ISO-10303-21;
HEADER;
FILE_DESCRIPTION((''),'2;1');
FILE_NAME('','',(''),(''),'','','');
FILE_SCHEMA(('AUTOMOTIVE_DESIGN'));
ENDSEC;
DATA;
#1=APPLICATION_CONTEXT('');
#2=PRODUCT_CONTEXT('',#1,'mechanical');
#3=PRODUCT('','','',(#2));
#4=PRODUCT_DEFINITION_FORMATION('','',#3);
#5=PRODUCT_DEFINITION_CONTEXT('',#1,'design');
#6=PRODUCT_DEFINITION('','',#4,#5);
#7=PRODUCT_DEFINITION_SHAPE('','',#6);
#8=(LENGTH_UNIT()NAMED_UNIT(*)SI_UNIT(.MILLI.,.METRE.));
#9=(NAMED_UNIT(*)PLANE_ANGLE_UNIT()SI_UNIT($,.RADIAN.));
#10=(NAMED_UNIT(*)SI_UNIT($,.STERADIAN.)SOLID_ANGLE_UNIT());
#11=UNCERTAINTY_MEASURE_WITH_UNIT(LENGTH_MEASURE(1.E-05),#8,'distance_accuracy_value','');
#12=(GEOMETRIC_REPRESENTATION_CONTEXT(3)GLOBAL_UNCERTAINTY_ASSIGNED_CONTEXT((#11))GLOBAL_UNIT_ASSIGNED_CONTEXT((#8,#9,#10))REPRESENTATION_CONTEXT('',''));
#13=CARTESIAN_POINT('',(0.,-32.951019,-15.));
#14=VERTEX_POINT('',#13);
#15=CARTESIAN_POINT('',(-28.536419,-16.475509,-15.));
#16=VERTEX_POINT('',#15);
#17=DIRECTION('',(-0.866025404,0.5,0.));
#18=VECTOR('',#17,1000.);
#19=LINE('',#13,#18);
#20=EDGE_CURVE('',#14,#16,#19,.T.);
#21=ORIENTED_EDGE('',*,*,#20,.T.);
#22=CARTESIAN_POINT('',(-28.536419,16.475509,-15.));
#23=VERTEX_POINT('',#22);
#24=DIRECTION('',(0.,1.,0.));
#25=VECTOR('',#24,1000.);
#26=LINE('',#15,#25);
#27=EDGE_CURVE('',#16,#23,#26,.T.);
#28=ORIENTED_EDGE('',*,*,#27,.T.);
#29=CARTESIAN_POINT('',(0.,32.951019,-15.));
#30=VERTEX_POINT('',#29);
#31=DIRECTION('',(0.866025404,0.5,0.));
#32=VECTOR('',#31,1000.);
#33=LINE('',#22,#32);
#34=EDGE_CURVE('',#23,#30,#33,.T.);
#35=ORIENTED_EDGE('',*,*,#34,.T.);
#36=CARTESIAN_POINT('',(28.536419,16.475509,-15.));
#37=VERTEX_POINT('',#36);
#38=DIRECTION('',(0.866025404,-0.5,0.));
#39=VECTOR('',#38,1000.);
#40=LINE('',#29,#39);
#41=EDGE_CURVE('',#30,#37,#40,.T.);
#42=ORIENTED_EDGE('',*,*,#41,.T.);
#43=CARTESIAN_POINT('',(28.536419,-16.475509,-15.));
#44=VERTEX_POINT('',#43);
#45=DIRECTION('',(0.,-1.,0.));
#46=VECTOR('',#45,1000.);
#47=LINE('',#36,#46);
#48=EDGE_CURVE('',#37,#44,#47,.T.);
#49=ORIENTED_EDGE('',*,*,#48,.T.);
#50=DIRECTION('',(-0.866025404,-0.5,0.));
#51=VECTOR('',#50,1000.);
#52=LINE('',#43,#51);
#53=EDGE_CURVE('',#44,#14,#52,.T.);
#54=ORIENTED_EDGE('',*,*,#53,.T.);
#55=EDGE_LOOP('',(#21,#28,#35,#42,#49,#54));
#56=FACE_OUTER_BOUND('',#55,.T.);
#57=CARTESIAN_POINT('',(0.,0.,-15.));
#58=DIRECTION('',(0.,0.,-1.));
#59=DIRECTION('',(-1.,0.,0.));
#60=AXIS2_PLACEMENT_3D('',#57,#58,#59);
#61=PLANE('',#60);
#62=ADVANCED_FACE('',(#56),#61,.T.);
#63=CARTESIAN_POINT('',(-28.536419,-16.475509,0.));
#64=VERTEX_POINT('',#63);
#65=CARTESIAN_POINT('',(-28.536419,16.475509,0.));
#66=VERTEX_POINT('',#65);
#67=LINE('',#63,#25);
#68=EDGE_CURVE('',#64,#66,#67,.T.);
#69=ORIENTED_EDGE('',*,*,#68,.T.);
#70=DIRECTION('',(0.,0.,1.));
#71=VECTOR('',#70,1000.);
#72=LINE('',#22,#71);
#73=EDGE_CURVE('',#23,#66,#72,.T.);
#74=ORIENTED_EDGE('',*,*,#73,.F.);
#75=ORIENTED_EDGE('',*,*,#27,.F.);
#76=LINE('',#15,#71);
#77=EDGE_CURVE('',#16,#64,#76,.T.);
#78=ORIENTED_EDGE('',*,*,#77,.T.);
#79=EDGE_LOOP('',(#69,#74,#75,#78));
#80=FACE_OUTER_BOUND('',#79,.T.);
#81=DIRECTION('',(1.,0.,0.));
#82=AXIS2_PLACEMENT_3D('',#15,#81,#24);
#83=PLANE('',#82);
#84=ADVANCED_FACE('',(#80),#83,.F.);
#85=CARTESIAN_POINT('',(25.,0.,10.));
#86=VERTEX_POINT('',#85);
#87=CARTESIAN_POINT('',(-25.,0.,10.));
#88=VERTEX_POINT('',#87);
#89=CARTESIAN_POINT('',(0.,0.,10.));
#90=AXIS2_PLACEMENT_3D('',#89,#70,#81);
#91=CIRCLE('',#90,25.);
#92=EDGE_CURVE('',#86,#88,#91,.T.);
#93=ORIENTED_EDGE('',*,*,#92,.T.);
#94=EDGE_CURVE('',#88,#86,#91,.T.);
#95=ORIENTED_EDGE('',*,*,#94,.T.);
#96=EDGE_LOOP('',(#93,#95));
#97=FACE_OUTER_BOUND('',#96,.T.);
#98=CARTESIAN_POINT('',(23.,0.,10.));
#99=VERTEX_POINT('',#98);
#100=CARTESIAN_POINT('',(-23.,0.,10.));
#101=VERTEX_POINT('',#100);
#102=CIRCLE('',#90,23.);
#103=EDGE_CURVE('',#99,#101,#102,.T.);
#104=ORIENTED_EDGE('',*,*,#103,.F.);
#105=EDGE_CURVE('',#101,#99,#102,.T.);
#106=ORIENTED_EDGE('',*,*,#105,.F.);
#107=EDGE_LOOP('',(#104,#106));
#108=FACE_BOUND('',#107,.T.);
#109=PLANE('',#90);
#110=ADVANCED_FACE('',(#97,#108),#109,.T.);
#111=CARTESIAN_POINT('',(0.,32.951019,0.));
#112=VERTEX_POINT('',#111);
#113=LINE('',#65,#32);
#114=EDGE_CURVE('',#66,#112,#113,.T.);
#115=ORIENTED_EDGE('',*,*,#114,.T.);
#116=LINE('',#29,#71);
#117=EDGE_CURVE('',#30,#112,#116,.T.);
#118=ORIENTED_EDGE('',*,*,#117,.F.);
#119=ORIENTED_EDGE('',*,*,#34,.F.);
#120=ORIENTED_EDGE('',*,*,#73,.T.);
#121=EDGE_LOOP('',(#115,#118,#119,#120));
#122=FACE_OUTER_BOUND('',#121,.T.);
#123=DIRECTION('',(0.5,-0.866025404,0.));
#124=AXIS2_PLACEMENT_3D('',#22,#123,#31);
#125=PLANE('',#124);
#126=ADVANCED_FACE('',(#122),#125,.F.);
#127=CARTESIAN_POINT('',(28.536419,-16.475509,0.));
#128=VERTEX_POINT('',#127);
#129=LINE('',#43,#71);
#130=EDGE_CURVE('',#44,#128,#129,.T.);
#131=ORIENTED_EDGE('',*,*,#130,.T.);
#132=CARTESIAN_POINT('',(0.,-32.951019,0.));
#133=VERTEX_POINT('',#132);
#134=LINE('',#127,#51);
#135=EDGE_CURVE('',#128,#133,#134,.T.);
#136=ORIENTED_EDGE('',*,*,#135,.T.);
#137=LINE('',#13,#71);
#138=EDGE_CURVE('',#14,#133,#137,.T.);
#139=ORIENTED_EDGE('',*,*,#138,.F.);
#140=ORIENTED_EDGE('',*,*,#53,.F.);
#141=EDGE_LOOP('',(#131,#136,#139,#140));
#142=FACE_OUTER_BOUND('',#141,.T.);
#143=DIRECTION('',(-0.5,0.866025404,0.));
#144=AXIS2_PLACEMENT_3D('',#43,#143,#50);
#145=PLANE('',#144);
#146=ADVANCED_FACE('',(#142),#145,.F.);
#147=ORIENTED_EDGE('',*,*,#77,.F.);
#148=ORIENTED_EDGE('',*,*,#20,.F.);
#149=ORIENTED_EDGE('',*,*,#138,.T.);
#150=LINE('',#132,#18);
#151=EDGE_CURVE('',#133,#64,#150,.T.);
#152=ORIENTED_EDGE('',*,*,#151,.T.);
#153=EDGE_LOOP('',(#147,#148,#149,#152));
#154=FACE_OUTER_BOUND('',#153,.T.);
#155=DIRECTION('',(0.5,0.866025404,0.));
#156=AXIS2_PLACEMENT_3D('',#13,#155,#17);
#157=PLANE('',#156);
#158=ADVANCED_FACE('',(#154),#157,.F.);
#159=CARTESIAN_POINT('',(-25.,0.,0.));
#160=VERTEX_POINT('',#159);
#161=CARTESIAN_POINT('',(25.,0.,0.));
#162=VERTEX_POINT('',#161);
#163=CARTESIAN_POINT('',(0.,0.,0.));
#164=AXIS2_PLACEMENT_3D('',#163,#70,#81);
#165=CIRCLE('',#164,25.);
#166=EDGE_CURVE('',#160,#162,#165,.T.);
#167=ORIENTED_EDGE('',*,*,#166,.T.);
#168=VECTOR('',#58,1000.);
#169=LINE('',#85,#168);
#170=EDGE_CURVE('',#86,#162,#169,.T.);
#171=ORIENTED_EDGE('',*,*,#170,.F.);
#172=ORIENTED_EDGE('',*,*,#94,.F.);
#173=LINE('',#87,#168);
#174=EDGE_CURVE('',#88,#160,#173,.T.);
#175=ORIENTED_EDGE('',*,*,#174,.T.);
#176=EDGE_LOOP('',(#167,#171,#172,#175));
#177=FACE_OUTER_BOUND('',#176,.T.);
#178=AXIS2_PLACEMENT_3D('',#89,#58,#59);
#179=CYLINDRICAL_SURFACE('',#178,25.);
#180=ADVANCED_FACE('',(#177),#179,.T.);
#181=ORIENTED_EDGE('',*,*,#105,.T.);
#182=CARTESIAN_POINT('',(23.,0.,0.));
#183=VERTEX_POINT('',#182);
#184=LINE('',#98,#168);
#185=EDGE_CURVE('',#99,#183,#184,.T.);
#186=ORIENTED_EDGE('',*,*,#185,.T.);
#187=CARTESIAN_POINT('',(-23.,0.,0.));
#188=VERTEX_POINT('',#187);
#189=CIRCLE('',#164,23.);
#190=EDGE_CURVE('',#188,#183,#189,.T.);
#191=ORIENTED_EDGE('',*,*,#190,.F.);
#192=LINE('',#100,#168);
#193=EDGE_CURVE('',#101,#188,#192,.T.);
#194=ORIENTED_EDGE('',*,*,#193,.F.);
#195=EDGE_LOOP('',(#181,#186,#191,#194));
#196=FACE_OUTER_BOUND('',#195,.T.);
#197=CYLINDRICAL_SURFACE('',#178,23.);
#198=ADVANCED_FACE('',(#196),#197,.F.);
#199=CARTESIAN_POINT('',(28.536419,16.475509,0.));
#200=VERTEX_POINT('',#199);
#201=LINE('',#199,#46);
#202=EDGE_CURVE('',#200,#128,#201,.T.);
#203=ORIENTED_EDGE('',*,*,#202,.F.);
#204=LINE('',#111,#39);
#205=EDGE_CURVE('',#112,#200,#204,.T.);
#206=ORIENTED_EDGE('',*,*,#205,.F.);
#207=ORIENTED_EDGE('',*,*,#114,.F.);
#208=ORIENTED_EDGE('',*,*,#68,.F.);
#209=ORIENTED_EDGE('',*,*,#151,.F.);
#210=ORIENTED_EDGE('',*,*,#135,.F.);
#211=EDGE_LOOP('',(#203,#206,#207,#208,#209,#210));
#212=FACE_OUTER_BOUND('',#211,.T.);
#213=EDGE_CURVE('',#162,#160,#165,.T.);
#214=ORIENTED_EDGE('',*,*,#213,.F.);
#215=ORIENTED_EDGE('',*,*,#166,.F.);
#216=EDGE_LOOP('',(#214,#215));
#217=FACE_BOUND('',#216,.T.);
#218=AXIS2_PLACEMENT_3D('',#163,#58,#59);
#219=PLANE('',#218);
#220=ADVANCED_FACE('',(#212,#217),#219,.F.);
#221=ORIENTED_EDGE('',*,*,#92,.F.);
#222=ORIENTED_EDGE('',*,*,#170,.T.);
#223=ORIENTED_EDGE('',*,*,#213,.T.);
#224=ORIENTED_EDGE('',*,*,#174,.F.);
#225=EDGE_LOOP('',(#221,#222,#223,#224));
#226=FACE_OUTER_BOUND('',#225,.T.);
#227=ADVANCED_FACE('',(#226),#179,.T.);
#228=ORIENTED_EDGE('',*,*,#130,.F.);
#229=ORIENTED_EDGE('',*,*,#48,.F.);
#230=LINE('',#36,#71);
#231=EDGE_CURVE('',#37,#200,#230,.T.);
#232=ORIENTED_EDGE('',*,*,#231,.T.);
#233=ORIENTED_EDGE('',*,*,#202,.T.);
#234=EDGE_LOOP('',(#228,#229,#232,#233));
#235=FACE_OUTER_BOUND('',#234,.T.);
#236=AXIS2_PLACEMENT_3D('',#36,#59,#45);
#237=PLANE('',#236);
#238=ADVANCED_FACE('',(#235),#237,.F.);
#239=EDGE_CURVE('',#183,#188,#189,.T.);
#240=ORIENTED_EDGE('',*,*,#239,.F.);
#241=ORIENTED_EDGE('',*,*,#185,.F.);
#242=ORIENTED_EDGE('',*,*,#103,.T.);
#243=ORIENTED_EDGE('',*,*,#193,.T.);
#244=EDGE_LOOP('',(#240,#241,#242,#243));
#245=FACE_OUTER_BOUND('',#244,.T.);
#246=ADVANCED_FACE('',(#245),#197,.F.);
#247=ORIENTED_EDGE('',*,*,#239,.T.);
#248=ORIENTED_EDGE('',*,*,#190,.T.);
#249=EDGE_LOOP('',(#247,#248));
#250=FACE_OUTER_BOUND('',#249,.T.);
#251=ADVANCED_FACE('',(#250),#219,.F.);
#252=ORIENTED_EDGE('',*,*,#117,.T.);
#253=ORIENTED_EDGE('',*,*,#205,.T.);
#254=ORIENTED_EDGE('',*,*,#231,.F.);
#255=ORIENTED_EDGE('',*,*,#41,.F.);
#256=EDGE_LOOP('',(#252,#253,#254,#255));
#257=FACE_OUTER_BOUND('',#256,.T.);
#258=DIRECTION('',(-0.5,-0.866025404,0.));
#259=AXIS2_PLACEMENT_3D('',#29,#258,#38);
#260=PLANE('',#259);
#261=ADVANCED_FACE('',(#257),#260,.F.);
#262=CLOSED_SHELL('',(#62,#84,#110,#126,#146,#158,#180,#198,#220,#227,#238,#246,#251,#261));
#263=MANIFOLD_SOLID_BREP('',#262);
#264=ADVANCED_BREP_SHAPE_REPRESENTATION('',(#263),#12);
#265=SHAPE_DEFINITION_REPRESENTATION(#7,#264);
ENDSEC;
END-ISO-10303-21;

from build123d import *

# Parameters (mm, degrees)
SKETCH1_R           = 25
SKETCH1_R_2         = 23
BOSS_EXTRUDE1_DEPTH = 10
BOSS_EXTRUDE2_DEPTH = 15


with BuildPart() as part:
    # Sketch1 → Boss-Extrude1 (new body)
    with BuildSketch(Plane.XY):
        Circle(SKETCH1_R)
        Circle(SKETCH1_R_2, mode=Mode.SUBTRACT)
    extrude(amount=BOSS_EXTRUDE1_DEPTH)

    # Sketch2 → Boss-Extrude2 (add)
    with BuildSketch(Plane(origin=(0, 0, 0), x_dir=(-1, 0, 0), z_dir=(0, 0, -1))):
        Polygon((0, 32.951018806), (-28.536419367, 16.475509403), (-28.536419367, -16.475509403), (0, -32.951018806), (28.536419367, -16.475509403), (28.536419367, 16.475509403), align=None)
    extrude(amount=BOSS_EXTRUDE2_DEPTH)


solid = part.part
